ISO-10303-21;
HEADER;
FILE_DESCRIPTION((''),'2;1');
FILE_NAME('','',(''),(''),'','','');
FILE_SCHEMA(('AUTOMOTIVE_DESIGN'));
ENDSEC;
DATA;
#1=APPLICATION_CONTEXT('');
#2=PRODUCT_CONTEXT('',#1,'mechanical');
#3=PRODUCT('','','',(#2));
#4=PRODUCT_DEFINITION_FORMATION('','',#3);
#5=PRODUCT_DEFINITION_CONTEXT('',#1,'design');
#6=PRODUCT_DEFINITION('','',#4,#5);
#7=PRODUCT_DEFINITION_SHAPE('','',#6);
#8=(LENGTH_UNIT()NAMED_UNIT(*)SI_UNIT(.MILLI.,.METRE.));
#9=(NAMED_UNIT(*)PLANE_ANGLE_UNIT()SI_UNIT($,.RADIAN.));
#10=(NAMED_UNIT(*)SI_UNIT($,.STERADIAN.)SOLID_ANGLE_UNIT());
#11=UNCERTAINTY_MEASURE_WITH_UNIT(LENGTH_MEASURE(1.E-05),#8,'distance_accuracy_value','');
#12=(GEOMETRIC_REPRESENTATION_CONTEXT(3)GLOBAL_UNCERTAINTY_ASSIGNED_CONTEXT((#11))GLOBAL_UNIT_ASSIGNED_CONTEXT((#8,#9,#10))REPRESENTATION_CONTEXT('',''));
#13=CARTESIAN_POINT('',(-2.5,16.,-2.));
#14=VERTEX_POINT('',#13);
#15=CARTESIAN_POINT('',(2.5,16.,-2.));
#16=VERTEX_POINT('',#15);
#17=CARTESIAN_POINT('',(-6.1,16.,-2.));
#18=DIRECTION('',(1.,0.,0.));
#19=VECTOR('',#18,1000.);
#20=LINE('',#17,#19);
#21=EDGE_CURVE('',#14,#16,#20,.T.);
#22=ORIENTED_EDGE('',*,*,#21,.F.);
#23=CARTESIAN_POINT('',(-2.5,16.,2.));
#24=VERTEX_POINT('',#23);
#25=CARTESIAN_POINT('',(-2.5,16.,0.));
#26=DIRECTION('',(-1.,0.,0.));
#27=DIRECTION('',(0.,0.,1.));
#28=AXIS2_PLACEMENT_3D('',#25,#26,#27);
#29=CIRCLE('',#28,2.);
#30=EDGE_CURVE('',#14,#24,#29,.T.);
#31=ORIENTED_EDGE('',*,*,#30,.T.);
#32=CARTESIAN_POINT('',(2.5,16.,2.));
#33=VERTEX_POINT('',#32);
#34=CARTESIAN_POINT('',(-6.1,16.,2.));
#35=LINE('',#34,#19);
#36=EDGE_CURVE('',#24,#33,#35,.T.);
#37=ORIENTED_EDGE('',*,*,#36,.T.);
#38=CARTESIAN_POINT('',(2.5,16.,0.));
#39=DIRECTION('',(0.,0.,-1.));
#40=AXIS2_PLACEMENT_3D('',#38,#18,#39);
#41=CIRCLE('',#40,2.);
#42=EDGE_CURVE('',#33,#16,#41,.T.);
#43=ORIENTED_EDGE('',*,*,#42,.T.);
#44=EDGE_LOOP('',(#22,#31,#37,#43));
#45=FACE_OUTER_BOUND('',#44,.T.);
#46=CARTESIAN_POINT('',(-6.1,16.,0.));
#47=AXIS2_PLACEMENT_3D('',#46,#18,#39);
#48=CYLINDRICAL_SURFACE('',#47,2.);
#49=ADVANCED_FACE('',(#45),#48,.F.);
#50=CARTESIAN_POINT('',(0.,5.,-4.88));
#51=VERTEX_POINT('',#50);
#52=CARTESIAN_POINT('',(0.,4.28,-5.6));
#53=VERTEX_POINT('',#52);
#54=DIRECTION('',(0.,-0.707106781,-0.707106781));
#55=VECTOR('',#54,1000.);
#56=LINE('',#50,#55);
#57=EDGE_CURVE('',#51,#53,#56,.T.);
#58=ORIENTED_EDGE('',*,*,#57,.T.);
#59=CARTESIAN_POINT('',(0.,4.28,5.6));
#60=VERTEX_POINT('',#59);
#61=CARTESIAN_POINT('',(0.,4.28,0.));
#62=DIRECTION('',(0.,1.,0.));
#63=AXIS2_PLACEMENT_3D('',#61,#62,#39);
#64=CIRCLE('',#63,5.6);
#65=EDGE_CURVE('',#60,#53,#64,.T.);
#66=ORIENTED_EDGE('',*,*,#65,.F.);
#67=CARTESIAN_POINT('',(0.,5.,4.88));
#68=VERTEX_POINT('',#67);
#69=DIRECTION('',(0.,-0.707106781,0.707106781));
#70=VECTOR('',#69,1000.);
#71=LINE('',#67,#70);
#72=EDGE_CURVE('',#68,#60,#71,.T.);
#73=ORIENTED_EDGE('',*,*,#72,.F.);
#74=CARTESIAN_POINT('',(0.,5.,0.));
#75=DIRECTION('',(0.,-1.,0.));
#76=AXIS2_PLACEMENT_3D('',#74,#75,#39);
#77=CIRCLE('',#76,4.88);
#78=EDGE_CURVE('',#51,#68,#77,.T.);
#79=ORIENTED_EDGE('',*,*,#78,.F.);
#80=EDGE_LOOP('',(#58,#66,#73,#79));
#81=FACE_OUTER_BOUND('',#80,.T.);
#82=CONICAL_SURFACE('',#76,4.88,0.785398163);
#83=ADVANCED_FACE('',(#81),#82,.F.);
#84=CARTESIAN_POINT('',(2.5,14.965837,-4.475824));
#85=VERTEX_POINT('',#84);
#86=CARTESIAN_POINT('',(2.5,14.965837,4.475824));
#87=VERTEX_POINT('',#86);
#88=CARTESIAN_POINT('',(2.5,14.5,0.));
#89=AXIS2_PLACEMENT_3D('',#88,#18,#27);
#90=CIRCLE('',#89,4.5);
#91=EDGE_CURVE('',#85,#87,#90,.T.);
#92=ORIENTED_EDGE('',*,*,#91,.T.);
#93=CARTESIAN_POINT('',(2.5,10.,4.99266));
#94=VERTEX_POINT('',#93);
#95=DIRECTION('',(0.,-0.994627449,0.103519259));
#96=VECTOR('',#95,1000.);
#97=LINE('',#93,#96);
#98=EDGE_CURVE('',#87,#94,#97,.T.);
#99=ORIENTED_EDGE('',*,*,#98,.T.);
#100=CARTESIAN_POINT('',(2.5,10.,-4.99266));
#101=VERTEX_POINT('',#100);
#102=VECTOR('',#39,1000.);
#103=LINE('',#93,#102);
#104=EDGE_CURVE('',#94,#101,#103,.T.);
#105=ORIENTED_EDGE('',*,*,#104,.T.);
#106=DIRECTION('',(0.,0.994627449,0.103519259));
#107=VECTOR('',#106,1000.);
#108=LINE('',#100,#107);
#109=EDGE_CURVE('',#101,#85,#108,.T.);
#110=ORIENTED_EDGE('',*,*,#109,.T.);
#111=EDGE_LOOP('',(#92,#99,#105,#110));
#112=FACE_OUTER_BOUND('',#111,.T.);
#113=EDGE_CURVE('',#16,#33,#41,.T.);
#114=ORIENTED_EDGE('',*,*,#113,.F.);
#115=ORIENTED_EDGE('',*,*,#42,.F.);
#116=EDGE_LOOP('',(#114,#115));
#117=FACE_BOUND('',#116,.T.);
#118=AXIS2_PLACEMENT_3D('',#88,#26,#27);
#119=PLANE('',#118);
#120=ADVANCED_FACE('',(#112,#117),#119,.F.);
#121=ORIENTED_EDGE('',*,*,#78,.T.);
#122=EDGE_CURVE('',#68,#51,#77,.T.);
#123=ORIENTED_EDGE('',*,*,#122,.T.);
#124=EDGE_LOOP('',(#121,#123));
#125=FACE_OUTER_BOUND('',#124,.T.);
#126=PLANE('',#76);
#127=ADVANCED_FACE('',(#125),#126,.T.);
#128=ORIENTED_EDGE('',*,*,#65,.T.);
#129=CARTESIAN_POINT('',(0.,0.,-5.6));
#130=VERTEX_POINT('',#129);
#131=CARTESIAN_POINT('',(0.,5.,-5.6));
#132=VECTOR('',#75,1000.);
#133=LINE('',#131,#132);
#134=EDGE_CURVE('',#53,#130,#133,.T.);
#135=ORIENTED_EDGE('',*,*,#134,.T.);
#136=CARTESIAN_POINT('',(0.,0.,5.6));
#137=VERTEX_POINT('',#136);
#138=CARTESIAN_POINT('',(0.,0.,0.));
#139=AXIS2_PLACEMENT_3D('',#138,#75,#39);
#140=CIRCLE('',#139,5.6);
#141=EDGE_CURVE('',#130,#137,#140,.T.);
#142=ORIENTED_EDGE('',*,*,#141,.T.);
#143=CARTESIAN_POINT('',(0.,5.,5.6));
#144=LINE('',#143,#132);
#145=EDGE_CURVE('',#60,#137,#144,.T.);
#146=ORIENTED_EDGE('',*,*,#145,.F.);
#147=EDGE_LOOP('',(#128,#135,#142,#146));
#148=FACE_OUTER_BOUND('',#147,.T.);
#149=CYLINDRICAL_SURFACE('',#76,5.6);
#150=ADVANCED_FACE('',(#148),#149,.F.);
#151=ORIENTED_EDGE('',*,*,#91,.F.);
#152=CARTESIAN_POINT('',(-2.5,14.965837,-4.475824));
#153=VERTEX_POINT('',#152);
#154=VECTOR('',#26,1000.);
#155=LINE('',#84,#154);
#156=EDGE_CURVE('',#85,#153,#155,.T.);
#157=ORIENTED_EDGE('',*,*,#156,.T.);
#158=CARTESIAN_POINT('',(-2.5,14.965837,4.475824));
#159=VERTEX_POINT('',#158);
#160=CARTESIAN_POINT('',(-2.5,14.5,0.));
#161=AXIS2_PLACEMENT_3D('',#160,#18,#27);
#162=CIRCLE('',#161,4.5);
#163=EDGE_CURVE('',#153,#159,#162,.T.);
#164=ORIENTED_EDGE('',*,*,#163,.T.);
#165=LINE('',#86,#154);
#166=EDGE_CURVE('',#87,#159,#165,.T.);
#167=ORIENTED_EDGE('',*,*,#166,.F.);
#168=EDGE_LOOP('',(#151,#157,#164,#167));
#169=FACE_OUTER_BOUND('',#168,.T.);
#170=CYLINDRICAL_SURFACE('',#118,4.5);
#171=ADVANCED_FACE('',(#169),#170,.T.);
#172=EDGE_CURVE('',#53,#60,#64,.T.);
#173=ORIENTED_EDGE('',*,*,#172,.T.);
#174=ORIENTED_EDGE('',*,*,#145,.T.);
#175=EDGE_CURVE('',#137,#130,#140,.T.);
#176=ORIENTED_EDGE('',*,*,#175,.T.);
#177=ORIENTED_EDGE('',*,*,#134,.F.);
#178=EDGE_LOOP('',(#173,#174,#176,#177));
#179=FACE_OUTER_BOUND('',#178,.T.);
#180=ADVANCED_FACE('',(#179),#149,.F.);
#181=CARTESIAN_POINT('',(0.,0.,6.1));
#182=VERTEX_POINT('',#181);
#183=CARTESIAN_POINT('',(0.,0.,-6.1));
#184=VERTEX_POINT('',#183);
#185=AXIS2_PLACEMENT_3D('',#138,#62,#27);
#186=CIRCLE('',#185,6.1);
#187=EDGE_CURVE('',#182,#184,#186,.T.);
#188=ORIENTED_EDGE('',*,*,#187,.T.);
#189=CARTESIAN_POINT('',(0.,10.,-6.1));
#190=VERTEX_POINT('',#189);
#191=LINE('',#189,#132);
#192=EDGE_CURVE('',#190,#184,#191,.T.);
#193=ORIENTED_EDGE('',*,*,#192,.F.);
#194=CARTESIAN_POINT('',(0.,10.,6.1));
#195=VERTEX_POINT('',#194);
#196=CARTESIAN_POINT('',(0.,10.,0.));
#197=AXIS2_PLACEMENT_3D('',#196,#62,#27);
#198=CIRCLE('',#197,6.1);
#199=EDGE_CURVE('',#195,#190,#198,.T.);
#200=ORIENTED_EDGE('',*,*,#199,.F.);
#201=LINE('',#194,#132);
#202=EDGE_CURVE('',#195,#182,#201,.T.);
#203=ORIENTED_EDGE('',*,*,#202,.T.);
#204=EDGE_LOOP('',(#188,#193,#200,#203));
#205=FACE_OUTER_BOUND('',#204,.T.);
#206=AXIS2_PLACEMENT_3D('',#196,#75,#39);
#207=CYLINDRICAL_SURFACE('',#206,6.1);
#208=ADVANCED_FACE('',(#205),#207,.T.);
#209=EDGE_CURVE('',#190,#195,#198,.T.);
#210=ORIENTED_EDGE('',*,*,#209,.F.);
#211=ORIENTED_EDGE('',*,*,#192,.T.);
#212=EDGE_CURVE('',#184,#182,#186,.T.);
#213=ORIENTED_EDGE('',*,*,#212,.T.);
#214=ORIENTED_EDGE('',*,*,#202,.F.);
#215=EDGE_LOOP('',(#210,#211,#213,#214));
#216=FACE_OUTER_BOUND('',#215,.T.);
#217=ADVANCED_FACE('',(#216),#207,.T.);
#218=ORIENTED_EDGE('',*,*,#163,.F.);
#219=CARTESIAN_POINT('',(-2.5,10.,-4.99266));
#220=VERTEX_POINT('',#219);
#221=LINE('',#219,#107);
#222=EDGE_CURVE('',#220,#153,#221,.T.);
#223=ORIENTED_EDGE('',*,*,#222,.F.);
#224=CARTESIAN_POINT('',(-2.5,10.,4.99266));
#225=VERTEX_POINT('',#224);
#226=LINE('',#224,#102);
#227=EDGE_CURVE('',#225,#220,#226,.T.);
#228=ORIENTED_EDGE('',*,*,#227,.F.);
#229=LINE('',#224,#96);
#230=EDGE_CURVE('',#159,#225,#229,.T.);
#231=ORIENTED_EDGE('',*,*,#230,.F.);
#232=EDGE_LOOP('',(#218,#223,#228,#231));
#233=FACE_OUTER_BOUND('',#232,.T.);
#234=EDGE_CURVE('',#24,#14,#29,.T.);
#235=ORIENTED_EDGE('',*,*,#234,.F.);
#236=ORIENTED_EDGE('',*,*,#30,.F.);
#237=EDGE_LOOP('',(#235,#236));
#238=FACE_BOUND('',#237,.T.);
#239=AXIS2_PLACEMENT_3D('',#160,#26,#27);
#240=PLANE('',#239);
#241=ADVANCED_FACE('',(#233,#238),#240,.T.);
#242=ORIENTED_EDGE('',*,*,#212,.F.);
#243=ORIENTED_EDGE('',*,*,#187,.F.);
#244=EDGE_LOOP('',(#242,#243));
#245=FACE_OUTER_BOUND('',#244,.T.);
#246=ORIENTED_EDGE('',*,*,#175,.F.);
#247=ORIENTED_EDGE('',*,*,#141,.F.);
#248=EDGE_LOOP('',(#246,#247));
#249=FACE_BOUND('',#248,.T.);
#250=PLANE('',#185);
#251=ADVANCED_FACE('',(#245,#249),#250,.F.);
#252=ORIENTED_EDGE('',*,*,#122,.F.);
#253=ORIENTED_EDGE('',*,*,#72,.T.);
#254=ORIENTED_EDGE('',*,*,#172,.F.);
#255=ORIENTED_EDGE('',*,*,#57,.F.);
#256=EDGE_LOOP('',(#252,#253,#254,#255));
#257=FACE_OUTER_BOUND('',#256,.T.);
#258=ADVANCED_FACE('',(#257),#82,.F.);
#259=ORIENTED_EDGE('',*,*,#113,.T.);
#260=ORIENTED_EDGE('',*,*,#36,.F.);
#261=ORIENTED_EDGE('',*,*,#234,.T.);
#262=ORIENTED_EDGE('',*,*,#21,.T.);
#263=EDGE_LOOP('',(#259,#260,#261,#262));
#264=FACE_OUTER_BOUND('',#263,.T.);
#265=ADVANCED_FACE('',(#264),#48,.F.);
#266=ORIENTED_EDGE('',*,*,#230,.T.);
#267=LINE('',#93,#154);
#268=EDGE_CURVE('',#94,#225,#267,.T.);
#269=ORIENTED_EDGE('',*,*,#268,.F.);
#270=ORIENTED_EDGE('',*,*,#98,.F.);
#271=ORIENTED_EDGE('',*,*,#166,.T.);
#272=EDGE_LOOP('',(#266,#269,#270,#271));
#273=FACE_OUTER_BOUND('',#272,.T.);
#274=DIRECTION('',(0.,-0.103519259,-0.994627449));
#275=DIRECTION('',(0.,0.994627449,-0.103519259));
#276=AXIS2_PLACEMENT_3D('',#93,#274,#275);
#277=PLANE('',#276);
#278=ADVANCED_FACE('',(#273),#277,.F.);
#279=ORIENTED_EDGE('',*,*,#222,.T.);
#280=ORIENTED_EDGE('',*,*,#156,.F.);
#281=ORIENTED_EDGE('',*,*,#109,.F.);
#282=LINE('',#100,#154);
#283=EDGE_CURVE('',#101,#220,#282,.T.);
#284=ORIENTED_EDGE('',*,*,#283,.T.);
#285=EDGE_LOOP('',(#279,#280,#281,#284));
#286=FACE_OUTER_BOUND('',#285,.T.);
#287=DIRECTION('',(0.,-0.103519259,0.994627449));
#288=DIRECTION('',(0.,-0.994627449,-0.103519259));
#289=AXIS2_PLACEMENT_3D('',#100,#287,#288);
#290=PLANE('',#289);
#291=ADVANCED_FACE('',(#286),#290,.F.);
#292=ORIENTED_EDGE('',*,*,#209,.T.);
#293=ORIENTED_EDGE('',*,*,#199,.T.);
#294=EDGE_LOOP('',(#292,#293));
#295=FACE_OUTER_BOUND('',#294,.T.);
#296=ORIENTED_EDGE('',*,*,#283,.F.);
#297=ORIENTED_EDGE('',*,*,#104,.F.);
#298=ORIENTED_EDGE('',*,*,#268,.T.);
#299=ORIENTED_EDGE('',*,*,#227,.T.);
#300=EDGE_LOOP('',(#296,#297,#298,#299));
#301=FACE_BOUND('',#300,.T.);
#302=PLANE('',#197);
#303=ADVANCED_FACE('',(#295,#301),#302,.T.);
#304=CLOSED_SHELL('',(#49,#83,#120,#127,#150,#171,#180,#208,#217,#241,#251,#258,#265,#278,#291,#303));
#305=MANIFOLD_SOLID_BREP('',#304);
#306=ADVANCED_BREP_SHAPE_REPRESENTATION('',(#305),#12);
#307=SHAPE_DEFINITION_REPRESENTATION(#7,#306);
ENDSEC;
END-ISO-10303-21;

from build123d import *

# Parameters (mm, degrees)
SKETCH1_R           = 6.1
BOSS_EXTRUDE1_DEPTH = 10
BOSS_EXTRUDE2_DEPTH = 2.5
SKETCH3_R           = 2
CUT_EXTRUDE1_DEPTH  = 22.729473072
SKETCH4_R           = 5.6
CUT_EXTRUDE2_DEPTH  = 5
CHAMFER1_SIZE       = 0.72


with BuildPart() as part:
    # Sketch1 → Boss-Extrude1 (new body)
    with BuildSketch(Plane(origin=(0, 0, 0), x_dir=(1, 0, 0), z_dir=(0, 1, 0))):
        with Locations(Location((0, 0, 0), (0, 0, 270))):
            Circle(SKETCH1_R)
    extrude(amount=BOSS_EXTRUDE1_DEPTH)

    # Sketch2 → Boss-Extrude2 (add, symmetric)
    with BuildSketch(Plane(origin=(0, 0, 0), x_dir=(0, 0, -1), z_dir=(1, 0, 0))):
        with BuildLine():
            Line((-4.992659986, 10), (-4.475823522, 14.965836668))
            ThreePointArc((-4.475823522, 14.965836668), (0, 19), (4.475823522, 14.965836668))
            Line((4.475823522, 14.965836668), (4.992659986, 10))
            Line((4.992659986, 10), (-4.992659986, 10))
        make_face()
    extrude(amount=BOSS_EXTRUDE2_DEPTH, both=True)

    # Sketch3 → Cut-Extrude1 (cut, through all)
    with BuildSketch(Plane(origin=(2.5, 0, 0), x_dir=(0, 0, -1), z_dir=(1, 0, 0))):
        with Locations((0, 16)):
            Circle(SKETCH3_R)
    extrude(amount=-CUT_EXTRUDE1_DEPTH, mode=Mode.SUBTRACT)

    # Sketch4 → Cut-Extrude2 (cut)
    with BuildSketch(Plane.XZ):
        with Locations(Location((0, 0, 0), (0, 0, 270))):
            Circle(SKETCH4_R)
    extrude(amount=-CUT_EXTRUDE2_DEPTH, mode=Mode.SUBTRACT)

    # Chamfer1
    chamfer1_edges = [part.edges().sort_by_distance(p)[0] for p in [
        (0, 5, 5.6),
    ]]
    chamfer(chamfer1_edges, length=CHAMFER1_SIZE)


solid = part.part
